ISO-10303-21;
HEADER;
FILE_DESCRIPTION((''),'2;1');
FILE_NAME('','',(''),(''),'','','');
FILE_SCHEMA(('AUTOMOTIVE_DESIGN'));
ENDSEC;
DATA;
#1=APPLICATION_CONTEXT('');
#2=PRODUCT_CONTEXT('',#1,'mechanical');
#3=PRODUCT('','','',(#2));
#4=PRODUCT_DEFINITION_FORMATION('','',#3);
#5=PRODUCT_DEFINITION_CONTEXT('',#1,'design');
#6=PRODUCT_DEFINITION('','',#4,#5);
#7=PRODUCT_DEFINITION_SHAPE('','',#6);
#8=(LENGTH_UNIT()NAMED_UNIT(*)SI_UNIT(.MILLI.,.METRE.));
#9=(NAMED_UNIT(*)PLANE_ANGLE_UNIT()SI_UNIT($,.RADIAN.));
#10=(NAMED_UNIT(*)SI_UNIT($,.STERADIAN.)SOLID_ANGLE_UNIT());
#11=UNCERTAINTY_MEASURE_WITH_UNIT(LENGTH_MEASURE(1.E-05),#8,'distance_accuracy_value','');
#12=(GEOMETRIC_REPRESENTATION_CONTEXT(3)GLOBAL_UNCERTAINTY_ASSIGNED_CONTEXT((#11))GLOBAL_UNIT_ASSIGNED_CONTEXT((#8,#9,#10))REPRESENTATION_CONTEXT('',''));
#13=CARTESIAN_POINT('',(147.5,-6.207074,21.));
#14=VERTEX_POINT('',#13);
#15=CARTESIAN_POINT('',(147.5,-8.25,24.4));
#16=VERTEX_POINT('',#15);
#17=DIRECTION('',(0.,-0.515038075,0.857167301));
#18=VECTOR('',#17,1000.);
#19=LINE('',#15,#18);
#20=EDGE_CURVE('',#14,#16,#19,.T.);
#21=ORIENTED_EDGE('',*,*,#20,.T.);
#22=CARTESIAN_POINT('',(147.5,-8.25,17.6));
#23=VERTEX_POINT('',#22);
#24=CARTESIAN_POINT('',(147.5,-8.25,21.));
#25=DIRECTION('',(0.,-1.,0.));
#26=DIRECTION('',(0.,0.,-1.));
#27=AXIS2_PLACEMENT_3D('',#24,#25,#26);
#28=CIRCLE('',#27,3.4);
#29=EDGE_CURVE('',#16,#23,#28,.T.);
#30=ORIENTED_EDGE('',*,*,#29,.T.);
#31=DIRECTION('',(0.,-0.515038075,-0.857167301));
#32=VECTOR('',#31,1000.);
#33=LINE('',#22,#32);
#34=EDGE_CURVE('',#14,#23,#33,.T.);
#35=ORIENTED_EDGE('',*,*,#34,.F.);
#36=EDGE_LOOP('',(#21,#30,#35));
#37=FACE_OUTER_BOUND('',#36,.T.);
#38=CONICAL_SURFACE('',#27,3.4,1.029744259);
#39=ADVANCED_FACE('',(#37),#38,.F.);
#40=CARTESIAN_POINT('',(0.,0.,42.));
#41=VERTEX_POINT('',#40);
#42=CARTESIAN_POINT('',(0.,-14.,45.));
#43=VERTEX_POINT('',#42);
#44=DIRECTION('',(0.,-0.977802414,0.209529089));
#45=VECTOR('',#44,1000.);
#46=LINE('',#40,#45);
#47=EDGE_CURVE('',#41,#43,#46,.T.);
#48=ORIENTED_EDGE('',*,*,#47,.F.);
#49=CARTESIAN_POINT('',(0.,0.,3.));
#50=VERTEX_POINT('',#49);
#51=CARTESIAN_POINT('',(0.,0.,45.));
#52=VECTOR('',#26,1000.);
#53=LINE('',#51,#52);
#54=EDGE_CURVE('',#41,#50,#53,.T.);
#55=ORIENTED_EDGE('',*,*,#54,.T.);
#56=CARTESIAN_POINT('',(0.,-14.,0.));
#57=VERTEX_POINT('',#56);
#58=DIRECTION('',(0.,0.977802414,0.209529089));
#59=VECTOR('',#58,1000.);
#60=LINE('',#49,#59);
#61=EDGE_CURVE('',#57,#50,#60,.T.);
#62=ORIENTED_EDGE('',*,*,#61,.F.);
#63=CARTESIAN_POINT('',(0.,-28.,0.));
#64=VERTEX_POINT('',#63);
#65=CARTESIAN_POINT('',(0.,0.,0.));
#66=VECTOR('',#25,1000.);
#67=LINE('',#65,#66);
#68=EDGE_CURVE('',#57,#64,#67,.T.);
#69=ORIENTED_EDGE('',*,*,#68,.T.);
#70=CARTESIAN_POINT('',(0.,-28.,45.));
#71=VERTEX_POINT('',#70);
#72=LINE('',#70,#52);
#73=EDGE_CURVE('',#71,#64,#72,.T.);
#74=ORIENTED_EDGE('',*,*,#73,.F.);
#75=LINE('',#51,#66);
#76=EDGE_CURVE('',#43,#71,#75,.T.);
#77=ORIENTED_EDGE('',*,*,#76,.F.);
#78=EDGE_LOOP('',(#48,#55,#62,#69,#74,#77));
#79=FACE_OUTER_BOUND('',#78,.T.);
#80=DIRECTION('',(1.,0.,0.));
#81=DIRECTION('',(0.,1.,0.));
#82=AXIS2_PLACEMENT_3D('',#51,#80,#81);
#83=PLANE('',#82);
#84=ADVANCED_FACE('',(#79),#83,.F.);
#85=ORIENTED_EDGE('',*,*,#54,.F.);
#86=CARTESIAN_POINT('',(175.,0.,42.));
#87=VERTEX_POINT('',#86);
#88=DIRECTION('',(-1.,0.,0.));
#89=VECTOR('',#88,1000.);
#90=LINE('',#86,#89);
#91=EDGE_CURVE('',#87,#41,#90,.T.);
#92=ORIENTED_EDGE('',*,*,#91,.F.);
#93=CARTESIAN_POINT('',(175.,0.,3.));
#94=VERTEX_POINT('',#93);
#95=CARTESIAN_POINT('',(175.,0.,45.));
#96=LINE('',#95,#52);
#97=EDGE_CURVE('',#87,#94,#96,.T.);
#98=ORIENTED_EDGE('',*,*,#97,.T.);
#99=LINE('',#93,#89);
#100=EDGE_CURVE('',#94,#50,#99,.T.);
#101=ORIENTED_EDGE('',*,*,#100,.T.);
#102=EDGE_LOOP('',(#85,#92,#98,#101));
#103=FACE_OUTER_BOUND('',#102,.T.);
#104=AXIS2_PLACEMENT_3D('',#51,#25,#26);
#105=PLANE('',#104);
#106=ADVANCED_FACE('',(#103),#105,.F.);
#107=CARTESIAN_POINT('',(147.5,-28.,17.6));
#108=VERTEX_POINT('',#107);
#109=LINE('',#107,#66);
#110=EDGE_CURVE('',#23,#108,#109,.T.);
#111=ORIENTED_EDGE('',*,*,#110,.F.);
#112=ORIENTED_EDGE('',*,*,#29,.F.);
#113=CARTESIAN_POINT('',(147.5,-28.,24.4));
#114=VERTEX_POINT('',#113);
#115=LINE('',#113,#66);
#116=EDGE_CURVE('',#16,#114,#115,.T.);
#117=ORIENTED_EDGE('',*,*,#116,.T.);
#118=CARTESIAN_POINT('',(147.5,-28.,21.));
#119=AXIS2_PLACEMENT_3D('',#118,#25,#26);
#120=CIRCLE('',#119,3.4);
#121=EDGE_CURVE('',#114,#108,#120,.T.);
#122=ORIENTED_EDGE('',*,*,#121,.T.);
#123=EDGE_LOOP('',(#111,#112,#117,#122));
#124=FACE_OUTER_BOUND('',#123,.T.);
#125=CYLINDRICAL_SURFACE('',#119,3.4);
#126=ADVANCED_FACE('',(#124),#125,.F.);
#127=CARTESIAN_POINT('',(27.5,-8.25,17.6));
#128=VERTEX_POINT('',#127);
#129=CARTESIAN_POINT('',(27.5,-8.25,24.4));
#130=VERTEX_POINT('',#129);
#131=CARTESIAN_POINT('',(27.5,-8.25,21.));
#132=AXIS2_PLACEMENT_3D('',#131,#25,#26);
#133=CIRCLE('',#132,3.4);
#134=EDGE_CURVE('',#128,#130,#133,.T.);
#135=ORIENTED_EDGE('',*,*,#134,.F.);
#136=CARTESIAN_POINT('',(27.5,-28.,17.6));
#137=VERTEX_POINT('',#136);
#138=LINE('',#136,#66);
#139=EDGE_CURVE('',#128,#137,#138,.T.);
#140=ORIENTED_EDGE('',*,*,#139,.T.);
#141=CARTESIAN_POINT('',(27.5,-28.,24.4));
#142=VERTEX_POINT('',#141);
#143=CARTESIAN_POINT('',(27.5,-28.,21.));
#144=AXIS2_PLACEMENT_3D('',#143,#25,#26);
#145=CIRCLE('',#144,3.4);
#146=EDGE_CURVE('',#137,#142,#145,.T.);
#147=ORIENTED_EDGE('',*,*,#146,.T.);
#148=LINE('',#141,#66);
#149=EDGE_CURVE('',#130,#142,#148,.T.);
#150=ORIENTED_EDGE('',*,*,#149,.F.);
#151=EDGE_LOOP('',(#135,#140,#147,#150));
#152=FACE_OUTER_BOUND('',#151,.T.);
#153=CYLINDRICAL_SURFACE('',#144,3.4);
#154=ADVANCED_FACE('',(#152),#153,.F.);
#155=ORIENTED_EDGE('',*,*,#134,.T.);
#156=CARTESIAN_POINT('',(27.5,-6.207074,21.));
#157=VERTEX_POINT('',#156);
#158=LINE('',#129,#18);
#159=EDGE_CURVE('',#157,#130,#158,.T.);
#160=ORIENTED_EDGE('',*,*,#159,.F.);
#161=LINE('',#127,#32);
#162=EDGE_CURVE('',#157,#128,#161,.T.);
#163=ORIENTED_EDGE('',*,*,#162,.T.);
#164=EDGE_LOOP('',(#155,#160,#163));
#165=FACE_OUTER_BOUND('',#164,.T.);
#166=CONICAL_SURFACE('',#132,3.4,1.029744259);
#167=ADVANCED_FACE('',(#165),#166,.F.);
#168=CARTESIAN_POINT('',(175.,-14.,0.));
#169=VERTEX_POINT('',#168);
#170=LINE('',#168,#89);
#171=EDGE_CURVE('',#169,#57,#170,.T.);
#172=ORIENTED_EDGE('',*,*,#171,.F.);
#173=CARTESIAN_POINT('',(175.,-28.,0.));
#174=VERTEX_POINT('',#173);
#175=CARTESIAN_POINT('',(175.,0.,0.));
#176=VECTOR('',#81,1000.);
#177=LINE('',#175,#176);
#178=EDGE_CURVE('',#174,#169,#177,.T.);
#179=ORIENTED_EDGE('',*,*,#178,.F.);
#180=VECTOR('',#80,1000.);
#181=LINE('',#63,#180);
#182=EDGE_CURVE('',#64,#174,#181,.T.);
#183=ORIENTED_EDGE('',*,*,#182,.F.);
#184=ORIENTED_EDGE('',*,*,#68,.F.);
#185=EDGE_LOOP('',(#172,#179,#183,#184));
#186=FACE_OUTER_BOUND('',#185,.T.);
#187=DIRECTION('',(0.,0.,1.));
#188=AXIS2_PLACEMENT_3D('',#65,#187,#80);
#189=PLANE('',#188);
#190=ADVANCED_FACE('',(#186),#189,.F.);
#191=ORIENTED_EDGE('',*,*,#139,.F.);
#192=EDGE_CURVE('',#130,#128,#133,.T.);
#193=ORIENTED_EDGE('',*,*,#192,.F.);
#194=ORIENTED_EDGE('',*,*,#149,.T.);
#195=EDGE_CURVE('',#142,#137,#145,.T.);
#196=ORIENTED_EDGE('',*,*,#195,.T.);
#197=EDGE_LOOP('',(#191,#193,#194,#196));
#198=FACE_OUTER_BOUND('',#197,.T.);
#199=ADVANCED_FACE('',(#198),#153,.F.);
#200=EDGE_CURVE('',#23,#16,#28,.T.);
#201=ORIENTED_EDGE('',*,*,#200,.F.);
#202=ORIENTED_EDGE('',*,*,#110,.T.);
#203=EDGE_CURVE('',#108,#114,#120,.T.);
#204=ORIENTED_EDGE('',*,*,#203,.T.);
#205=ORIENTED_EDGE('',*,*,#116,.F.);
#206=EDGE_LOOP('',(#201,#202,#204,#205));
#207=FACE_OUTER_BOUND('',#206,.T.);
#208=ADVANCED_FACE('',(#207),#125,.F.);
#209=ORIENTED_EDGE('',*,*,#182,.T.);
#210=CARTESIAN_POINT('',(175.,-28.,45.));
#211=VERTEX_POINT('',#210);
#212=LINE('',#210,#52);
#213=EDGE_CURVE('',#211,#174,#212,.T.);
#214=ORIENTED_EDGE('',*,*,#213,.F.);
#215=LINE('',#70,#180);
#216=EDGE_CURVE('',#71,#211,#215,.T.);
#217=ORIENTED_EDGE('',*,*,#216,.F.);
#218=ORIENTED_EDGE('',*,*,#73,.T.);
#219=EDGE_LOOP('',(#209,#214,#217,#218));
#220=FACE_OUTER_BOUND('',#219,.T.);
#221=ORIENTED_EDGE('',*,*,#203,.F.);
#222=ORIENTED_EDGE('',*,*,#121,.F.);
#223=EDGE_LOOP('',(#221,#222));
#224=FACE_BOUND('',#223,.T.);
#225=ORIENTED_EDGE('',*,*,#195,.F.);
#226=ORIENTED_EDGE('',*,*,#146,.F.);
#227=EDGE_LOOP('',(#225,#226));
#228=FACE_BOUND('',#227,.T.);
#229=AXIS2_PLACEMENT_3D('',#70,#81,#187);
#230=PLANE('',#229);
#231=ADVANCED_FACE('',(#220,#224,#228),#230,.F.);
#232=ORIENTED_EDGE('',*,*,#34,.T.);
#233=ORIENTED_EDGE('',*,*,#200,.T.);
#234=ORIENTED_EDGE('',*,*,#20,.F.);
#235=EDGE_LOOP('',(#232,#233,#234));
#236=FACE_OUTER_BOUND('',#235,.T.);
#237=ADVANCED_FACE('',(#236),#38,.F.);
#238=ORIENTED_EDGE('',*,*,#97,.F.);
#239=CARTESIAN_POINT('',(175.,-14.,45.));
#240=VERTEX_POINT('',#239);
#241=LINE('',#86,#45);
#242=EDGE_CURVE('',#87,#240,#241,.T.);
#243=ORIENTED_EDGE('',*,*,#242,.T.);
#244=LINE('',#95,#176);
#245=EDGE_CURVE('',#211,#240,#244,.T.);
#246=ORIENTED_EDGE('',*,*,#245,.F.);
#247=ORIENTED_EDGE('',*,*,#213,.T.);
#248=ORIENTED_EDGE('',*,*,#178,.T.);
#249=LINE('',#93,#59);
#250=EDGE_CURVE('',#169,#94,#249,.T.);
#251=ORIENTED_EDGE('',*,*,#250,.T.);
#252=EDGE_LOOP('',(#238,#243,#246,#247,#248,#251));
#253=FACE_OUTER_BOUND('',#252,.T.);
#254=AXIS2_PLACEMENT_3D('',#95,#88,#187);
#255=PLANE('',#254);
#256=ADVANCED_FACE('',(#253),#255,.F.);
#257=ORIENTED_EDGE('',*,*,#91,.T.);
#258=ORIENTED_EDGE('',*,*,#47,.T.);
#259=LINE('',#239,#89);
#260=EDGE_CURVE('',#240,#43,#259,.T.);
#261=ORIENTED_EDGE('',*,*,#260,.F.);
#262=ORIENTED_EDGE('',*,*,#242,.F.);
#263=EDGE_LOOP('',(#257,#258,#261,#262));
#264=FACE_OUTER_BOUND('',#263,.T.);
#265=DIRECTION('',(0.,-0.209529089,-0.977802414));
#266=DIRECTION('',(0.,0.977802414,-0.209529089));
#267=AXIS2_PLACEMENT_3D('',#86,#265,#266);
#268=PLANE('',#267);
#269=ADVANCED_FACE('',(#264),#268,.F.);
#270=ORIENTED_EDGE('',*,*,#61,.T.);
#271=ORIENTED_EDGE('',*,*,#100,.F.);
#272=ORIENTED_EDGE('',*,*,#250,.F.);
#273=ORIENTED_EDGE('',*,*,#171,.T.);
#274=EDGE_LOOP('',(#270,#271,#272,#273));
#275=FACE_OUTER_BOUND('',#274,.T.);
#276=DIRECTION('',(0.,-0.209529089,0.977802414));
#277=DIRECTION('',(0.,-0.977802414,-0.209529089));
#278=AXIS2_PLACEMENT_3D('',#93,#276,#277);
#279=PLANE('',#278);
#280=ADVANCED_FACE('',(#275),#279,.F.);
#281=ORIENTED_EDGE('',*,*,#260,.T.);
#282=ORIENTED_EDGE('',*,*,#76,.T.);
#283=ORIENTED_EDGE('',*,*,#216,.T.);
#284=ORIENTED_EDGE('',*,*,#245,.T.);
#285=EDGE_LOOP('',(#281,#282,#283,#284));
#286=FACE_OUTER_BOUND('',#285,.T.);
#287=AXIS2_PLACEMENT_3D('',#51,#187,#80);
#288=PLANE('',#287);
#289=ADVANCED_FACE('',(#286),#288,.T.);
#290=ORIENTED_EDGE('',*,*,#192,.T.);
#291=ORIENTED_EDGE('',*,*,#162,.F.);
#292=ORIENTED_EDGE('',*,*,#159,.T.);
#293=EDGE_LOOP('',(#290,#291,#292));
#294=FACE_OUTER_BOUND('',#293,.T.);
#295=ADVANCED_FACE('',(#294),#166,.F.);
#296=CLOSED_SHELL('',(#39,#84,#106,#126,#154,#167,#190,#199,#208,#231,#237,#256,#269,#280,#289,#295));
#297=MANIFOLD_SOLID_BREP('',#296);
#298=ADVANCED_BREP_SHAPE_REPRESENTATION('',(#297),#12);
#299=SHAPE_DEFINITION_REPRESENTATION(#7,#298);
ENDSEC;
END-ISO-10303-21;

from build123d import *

# Parameters (mm, degrees)
SKETCH1_W             = 175
SKETCH1_H             = 28
BOSS_EXTRUDE1_DEPTH   = 45
M8_TAPPED_HOLE1_D     = 6.8
M8_TAPPED_HOLE1_DEPTH = 19.75
M8_TAPPED_HOLE1_TIP   = 2.042926105
CUT_EXTRUDE1_DEPTH    = 183.849665026


with BuildPart() as part:
    # Sketch1 → Boss-Extrude1 (new body)
    with BuildSketch(Plane.XY):
        with Locations((87.5, -14)):
            Rectangle(SKETCH1_W, SKETCH1_H)
    extrude(amount=BOSS_EXTRUDE1_DEPTH)

    # M8 Tapped Hole1
    with Locations(Plane(origin=(0, -28, 0), x_dir=(-1, 0, 0), z_dir=(0, -1, 0))):
        with Locations((-27.5, -21), (-147.5, -21)):
            Hole(M8_TAPPED_HOLE1_D / 2, depth=M8_TAPPED_HOLE1_DEPTH)
            with Locations((0, 0, -(M8_TAPPED_HOLE1_DEPTH + M8_TAPPED_HOLE1_TIP / 2))):  # 118° drill point
                Cone(0, M8_TAPPED_HOLE1_D / 2, M8_TAPPED_HOLE1_TIP, mode=Mode.SUBTRACT)

    # Sketch7 → Cut-Extrude1 (cut, through all)
    with BuildSketch(Plane.ZY):
        Polygon((3, 0), (0, -14), (0, 0), align=None)
        Polygon((45, 0), (42, 0), (45, -14), align=None)
    extrude(amount=-CUT_EXTRUDE1_DEPTH, mode=Mode.SUBTRACT)


solid = part.part
